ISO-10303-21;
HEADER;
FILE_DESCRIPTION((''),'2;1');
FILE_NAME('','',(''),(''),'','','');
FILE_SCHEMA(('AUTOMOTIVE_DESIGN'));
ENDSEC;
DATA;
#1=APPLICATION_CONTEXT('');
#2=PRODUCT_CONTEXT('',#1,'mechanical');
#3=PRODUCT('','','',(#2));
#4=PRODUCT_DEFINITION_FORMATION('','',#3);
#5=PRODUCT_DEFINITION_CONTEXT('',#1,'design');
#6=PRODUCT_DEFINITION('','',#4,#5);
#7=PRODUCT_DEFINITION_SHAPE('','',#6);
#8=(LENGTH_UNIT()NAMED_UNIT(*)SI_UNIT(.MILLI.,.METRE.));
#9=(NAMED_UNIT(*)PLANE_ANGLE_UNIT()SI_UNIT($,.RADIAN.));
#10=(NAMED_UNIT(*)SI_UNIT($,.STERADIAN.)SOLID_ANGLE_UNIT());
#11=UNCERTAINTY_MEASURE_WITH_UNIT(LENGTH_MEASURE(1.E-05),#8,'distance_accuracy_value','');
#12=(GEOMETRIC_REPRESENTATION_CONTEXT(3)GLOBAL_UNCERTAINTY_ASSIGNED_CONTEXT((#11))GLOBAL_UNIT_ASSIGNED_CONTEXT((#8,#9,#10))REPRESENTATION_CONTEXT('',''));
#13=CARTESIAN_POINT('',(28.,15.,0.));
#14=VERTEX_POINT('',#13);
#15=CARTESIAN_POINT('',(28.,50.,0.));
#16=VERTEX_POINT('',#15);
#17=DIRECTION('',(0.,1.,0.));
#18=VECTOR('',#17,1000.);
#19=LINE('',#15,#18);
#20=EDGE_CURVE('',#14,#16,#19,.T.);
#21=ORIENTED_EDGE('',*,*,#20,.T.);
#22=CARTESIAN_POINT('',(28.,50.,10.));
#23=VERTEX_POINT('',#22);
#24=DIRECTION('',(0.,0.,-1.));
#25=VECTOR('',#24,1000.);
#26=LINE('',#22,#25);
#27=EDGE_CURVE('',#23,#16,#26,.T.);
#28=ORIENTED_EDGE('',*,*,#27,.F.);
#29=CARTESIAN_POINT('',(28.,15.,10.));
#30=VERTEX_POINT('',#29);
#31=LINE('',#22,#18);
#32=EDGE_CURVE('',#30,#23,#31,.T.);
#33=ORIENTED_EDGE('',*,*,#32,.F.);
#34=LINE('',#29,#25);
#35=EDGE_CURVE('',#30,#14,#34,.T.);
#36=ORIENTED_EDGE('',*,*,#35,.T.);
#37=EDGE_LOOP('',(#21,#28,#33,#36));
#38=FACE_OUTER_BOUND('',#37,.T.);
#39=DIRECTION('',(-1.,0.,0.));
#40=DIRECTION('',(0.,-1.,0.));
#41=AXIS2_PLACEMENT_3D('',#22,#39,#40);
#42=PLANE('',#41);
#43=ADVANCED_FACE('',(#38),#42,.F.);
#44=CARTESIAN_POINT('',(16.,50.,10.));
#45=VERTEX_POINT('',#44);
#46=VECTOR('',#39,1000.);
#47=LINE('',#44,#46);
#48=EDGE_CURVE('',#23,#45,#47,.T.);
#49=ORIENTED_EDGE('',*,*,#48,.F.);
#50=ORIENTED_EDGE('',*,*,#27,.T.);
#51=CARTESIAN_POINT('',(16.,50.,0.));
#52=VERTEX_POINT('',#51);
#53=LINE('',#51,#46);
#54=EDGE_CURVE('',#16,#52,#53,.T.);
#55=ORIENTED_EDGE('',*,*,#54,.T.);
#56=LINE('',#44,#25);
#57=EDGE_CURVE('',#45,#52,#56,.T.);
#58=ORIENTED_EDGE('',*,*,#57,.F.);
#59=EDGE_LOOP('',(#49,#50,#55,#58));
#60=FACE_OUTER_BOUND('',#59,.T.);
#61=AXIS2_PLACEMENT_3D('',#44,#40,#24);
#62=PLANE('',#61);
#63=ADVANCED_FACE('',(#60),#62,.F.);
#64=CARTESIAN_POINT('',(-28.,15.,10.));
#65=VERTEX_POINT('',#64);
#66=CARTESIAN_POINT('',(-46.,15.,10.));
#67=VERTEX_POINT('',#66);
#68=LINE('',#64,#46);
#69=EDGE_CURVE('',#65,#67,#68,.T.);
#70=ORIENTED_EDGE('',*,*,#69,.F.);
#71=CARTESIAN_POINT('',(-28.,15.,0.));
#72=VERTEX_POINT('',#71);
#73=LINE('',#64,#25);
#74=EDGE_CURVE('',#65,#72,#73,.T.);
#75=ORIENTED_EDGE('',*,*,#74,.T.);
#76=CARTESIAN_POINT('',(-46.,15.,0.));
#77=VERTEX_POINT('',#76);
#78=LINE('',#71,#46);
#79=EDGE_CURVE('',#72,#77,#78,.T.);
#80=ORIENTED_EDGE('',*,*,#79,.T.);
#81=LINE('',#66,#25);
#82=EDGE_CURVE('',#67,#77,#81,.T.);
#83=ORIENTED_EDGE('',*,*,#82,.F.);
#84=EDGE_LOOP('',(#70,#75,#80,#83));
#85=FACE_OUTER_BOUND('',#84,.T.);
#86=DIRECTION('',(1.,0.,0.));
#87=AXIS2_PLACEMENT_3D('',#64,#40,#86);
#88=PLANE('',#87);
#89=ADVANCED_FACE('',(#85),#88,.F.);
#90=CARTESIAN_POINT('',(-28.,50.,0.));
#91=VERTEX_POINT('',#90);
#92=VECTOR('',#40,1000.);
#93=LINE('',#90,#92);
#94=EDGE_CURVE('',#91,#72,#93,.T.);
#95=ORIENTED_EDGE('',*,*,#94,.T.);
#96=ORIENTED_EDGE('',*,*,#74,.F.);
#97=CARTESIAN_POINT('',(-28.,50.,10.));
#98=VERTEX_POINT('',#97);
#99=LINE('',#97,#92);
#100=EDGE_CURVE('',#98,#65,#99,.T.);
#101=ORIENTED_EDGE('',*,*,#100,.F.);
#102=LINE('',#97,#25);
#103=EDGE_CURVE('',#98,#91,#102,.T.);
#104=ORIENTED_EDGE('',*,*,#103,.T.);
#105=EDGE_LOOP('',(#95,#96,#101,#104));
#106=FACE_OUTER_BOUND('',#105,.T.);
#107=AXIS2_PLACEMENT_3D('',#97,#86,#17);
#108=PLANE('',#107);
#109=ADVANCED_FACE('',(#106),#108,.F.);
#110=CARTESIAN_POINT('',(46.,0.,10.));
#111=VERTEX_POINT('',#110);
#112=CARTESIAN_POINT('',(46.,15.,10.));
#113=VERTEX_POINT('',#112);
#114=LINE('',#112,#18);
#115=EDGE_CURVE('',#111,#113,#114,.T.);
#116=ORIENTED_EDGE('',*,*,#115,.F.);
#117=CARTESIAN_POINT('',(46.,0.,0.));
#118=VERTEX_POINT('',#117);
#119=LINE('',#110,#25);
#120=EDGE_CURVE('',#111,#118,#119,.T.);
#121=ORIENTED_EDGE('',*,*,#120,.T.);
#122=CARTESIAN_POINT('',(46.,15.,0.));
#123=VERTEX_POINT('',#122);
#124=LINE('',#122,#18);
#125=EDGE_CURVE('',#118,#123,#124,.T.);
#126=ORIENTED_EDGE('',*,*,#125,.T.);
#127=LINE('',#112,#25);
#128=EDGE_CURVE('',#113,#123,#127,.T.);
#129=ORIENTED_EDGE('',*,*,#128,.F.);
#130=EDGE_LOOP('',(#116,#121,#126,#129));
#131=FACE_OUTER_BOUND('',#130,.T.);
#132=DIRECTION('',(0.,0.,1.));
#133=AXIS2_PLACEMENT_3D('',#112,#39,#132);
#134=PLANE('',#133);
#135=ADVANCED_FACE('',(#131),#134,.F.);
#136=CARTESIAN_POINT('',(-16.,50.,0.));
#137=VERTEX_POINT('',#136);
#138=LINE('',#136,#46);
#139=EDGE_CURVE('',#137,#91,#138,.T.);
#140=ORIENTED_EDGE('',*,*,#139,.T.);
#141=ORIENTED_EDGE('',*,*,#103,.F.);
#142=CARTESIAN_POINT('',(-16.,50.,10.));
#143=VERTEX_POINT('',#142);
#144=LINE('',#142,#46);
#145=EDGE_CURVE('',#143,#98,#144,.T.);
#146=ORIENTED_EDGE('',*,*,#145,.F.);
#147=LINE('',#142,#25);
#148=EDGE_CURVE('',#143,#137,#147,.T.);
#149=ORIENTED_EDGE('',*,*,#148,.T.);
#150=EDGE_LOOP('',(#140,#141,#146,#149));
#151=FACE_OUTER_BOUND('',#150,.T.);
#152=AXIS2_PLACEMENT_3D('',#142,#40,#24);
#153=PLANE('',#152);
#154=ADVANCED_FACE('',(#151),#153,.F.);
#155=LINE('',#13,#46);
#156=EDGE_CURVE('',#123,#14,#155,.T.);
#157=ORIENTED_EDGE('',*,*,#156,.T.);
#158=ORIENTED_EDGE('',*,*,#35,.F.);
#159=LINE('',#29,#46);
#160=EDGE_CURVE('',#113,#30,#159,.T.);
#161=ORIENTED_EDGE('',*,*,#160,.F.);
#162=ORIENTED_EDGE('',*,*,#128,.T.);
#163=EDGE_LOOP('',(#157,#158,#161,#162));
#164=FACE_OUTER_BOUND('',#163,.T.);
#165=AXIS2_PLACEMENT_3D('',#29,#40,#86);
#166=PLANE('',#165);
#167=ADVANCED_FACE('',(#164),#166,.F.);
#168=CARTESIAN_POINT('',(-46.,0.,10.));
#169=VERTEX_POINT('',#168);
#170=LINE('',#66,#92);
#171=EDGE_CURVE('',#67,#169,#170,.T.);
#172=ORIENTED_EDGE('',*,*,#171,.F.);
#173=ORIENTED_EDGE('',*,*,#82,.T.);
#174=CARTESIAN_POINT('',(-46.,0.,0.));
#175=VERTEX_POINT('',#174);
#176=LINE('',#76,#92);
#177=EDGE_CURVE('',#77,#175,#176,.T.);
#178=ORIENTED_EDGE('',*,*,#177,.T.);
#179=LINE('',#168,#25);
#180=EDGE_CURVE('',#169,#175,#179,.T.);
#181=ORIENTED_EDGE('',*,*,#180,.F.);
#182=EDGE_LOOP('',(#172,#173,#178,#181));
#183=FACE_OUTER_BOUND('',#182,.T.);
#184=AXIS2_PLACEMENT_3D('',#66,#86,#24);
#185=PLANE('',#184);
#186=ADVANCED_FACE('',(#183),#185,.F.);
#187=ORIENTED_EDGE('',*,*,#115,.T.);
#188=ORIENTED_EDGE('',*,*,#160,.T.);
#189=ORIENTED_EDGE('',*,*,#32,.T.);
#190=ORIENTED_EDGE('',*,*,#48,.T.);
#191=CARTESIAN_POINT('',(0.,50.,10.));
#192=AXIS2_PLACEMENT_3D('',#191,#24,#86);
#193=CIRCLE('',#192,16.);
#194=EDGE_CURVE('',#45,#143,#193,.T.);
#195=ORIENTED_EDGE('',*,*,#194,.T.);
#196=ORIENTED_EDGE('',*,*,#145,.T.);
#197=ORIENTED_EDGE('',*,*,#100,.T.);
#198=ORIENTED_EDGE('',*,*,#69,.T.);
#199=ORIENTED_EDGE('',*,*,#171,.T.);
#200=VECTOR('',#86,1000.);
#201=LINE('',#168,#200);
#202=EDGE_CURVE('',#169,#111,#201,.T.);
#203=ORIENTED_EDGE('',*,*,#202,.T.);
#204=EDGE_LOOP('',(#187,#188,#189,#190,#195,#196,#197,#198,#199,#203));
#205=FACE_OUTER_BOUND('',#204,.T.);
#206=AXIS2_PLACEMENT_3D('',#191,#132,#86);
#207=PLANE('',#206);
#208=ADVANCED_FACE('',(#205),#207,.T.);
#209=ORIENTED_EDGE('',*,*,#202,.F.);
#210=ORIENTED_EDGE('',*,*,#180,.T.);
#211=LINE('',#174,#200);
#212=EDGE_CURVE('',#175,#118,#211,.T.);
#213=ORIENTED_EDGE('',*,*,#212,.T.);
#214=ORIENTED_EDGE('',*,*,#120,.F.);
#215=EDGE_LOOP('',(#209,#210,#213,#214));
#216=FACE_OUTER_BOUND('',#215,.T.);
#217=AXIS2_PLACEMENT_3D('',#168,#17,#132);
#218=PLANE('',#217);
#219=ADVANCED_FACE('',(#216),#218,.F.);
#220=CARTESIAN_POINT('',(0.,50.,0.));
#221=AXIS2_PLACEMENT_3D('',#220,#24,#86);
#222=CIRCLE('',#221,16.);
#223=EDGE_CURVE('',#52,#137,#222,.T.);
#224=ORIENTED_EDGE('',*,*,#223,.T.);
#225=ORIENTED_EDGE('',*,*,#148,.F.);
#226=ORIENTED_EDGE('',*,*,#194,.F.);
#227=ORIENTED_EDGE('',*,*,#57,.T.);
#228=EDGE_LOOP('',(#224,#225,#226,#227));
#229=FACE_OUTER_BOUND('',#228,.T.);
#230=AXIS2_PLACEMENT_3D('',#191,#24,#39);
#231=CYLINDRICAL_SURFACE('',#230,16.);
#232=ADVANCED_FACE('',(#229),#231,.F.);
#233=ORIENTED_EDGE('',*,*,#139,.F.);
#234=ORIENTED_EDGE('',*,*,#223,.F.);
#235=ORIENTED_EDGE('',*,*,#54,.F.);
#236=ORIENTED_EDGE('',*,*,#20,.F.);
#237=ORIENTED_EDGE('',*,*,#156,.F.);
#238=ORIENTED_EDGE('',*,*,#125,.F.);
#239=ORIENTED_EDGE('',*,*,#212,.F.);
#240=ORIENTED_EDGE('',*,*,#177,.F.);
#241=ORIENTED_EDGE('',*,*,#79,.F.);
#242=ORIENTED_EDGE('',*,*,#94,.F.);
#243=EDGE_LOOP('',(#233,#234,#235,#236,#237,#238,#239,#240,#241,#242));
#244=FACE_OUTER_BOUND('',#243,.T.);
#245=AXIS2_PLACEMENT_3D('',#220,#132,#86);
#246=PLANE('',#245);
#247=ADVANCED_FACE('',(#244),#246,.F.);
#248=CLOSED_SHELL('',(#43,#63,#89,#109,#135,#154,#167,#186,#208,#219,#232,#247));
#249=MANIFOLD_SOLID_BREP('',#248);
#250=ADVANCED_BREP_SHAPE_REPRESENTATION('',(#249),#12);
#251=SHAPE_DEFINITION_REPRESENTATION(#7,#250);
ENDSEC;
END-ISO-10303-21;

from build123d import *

# Parameters (mm, degrees)
BOSS_EXTRUDE1_DEPTH = 10


with BuildPart() as part:
    # Sketch1 → Boss-Extrude1 (new body)
    with BuildSketch(Plane.XY):
        with BuildLine():
            Line((-16, 50), (-28, 50))
            Line((-28, 50), (-28, 15))
            Line((-28, 15), (-46, 15))
            Line((-46, 15), (-46, 0))
            Line((-46, 0), (46, 0))
            Line((46, 0), (46, 15))
            Line((46, 15), (28, 15))
            Line((28, 15), (28, 50))
            Line((28, 50), (16, 50))
            ThreePointArc((16, 50), (0, 34), (-16, 50))
        make_face()
    extrude(amount=BOSS_EXTRUDE1_DEPTH)


solid = part.part
